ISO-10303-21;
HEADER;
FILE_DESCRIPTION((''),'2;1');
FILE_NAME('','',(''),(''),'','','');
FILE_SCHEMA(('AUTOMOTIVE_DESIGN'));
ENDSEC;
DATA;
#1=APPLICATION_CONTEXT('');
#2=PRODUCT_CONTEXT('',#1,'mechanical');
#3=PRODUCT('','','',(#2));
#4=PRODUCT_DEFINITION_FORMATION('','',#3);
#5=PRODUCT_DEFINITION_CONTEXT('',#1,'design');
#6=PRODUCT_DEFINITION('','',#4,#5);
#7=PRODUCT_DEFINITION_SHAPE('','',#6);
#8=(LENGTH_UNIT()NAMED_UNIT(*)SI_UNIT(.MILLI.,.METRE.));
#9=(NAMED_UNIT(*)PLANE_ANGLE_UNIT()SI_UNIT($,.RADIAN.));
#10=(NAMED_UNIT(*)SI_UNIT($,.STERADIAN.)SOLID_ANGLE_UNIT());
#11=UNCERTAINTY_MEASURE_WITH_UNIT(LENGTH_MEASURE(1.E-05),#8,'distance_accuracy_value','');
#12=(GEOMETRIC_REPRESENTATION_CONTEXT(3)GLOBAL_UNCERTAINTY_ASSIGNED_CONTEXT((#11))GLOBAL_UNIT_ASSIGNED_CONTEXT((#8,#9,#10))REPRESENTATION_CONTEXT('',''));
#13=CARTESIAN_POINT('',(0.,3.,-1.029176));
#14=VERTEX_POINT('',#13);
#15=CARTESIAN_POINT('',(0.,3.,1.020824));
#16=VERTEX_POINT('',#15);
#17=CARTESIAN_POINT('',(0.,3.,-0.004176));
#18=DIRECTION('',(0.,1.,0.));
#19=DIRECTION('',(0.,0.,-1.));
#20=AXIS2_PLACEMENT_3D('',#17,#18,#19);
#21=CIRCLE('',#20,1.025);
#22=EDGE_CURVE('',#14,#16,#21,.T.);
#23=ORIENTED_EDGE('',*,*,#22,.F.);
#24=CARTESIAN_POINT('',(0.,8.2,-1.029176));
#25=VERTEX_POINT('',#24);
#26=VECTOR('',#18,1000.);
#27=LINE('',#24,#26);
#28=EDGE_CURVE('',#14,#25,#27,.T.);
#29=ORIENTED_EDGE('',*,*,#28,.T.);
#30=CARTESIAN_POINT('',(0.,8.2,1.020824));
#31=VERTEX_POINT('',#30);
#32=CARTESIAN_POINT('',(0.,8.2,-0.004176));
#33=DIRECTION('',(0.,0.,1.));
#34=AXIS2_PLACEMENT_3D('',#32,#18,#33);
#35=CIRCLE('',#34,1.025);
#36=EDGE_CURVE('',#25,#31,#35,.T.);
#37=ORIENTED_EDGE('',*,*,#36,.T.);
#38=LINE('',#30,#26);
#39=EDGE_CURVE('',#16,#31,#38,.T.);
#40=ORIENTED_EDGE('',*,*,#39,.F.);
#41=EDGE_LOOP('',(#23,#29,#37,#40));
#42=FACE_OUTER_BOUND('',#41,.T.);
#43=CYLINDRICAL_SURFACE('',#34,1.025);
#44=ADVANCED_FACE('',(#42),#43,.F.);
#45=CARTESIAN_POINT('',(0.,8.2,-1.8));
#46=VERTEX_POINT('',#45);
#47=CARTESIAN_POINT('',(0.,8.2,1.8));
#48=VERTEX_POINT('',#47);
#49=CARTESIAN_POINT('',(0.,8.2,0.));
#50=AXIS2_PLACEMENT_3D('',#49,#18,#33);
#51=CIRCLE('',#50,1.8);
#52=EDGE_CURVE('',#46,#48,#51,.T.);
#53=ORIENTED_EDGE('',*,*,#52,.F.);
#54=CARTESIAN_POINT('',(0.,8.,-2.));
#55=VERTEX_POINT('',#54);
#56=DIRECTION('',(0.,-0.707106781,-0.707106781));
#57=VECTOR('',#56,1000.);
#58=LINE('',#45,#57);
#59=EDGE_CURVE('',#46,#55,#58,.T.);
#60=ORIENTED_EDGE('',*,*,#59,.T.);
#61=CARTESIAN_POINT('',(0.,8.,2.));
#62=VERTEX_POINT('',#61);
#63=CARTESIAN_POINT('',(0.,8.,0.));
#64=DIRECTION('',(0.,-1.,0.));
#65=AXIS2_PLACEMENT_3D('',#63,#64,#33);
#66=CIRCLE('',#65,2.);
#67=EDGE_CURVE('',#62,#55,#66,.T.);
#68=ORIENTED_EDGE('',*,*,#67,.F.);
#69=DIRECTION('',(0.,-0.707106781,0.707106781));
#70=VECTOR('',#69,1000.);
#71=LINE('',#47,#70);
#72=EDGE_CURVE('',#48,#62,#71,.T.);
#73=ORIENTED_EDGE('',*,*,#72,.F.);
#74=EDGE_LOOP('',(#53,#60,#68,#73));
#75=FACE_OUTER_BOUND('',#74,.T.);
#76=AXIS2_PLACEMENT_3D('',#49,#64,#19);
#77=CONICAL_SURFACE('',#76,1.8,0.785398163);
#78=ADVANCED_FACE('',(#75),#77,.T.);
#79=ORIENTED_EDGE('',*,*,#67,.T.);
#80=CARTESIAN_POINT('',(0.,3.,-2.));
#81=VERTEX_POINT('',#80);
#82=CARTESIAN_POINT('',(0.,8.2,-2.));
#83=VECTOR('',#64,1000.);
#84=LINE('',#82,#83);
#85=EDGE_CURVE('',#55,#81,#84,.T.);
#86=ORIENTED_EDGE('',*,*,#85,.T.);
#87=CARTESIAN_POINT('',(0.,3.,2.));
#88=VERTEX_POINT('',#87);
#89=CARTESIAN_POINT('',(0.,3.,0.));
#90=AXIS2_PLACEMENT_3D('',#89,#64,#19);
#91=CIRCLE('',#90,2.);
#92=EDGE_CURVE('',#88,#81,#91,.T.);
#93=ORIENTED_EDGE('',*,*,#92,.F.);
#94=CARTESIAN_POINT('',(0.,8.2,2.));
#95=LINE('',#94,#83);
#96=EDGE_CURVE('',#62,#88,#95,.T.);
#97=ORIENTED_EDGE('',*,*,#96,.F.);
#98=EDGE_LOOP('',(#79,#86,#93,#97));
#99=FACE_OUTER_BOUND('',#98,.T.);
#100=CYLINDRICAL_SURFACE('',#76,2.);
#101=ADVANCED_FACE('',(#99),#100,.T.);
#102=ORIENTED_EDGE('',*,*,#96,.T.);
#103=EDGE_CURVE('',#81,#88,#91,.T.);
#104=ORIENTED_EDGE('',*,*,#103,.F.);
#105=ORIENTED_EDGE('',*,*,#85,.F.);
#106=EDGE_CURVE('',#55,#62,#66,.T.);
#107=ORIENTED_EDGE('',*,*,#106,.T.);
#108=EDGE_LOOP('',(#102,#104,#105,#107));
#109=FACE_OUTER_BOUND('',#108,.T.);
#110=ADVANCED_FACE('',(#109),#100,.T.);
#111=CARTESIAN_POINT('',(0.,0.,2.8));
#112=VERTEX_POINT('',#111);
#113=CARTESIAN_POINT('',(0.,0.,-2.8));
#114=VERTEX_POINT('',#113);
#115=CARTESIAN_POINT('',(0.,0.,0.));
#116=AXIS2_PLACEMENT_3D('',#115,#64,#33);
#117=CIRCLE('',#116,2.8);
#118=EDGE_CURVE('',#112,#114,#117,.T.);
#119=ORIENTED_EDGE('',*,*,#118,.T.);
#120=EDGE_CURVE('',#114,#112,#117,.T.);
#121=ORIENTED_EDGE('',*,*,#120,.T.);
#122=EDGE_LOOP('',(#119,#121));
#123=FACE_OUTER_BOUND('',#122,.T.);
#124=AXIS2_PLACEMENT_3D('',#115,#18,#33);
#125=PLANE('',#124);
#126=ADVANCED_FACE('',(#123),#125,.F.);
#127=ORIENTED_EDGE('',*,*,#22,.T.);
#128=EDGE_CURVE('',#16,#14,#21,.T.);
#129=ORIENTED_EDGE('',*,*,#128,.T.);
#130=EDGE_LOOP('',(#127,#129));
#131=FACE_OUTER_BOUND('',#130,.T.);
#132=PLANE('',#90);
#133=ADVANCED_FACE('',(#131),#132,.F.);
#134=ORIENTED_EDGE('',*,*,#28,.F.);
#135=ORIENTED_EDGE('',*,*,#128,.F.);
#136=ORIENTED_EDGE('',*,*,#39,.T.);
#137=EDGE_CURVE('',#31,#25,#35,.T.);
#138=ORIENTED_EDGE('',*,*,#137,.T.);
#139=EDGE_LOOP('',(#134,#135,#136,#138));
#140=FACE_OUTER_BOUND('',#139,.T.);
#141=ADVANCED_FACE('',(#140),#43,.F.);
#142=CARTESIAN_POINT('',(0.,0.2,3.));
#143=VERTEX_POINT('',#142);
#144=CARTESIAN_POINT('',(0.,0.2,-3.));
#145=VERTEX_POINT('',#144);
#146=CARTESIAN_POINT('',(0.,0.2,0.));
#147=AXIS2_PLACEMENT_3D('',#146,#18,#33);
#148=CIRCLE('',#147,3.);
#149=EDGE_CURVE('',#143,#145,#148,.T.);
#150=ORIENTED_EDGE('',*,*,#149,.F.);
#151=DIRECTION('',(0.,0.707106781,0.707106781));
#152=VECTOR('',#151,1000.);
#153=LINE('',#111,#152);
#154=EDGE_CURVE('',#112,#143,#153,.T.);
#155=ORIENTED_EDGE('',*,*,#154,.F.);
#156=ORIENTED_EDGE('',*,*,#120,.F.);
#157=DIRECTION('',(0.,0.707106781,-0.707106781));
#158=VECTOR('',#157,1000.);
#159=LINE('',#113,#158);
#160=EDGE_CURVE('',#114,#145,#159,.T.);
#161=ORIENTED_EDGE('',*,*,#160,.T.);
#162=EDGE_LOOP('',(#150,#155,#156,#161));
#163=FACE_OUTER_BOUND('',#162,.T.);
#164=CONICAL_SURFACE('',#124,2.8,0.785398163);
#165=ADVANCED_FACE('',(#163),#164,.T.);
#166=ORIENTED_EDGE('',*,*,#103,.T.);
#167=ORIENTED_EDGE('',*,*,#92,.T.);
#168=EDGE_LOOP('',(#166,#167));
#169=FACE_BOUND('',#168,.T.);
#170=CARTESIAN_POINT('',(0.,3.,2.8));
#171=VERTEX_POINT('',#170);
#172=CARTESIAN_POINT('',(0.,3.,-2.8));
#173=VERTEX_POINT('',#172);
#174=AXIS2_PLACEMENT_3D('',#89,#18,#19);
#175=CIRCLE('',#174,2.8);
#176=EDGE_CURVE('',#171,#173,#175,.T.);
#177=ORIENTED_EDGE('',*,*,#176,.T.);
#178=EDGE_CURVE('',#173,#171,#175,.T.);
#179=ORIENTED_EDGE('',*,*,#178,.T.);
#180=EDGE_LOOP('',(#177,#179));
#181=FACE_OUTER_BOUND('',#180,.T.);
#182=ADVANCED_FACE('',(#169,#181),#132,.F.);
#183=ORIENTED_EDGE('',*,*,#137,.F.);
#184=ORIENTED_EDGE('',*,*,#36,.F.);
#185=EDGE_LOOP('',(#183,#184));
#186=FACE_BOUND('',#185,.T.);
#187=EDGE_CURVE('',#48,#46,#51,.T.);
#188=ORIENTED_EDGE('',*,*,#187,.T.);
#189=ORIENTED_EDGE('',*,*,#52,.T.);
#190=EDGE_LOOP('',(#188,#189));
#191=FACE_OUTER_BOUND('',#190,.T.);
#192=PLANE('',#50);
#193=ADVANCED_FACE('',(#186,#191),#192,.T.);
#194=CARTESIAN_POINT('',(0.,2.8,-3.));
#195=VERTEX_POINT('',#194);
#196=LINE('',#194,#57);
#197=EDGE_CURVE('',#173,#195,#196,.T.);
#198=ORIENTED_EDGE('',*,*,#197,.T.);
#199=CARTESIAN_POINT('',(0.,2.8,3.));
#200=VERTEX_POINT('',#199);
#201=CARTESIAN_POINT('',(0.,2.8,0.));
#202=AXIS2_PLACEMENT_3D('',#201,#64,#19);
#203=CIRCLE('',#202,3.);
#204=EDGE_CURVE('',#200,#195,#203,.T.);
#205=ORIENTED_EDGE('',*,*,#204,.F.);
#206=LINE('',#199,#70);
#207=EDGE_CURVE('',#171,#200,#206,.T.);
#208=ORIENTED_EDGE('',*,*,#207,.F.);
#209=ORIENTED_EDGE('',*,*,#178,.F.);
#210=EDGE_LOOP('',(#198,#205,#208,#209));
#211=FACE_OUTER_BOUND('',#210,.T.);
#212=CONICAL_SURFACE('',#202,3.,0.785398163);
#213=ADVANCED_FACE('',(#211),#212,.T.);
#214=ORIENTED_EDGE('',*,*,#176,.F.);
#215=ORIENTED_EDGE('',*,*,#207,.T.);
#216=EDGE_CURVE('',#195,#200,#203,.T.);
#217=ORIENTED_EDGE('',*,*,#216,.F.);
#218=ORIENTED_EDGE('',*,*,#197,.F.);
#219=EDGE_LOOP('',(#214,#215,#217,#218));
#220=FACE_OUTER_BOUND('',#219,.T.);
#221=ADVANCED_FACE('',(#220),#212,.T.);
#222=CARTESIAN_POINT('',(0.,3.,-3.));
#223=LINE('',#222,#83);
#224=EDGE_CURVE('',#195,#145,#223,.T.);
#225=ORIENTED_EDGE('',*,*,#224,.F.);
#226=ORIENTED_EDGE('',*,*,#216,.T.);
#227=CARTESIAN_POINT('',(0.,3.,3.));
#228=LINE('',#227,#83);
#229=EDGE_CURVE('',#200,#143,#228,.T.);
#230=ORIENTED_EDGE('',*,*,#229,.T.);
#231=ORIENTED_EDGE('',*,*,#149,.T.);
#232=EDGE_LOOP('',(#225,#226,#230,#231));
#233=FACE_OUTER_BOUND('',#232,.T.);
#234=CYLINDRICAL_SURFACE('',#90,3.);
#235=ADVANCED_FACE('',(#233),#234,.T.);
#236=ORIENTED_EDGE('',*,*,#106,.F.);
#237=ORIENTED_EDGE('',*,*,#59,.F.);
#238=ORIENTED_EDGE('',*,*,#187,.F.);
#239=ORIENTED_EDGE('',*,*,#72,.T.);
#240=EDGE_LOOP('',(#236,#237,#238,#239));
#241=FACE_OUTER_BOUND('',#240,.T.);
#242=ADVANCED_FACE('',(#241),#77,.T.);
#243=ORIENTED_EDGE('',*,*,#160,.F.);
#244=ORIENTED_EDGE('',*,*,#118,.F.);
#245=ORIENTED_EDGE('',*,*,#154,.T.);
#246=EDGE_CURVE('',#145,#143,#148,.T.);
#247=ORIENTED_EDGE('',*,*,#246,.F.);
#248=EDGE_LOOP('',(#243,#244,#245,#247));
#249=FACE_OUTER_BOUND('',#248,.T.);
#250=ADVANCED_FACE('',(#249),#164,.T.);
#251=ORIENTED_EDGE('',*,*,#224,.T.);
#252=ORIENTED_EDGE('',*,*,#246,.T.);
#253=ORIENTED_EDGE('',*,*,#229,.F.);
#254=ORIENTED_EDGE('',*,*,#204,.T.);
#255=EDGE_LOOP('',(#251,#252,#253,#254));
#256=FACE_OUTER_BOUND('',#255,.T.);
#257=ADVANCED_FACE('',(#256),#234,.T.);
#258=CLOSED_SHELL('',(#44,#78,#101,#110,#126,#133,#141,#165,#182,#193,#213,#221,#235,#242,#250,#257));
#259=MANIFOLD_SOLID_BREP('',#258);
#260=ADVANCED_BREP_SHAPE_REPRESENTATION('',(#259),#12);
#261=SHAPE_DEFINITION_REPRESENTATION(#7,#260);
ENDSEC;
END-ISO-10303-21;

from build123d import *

# Parameters (mm, degrees)
SKETCH1_R               = 2
BOSS_EXTRUDE1_DEPTH     = 8.2
M2_5_TAPPED_HOLE1_D     = 2.05
M2_5_TAPPED_HOLE1_DEPTH = 6.35
M2_5_TAPPED_HOLE1_TIP   = 0.615882135
SKETCH8_R               = 3
BOSS_EXTRUDE2_DEPTH     = 3
CHAMFER1_SIZE           = 0.2
CHAMFER2_SIZE           = 0.2


with BuildPart() as part:
    # Sketch1 → Boss-Extrude1 (new body)
    with BuildSketch(Plane(origin=(0, 0, 0), x_dir=(1, 0, 0), z_dir=(0, 1, 0))):
        with Locations(Location((0, 0, 0), (0, 0, 270))):
            Circle(SKETCH1_R)
    extrude(amount=BOSS_EXTRUDE1_DEPTH)

    # M2.5 Tapped Hole1
    with Locations(Plane(origin=(0, 8.2, 0), x_dir=(1, 0, 0), z_dir=(0, 1, 0))):
        with Locations((0, 0.004175621)):
            Hole(M2_5_TAPPED_HOLE1_D / 2, depth=M2_5_TAPPED_HOLE1_DEPTH)
            with Locations((0, 0, -(M2_5_TAPPED_HOLE1_DEPTH + M2_5_TAPPED_HOLE1_TIP / 2))):  # 118° drill point
                Cone(0, M2_5_TAPPED_HOLE1_D / 2, M2_5_TAPPED_HOLE1_TIP, mode=Mode.SUBTRACT)

    # Sketch8 → Boss-Extrude2 (add)
    with BuildSketch(Plane.XZ):
        with Locations(Location((0, 0, 0), (0, 0, 270))):
            Circle(SKETCH8_R)
    extrude(amount=-BOSS_EXTRUDE2_DEPTH)

    # Chamfer1
    chamfer1_edges = [part.edges().sort_by_distance(p)[0] for p in [
        (0, 8.2, -2),
    ]]
    chamfer(chamfer1_edges, length=CHAMFER1_SIZE)

    # Chamfer2
    chamfer2_edges = [part.edges().sort_by_distance(p)[0] for p in [
        (0, 0, 3),
        (0, 3, 3),
    ]]
    chamfer(chamfer2_edges, length=CHAMFER2_SIZE)


solid = part.part
